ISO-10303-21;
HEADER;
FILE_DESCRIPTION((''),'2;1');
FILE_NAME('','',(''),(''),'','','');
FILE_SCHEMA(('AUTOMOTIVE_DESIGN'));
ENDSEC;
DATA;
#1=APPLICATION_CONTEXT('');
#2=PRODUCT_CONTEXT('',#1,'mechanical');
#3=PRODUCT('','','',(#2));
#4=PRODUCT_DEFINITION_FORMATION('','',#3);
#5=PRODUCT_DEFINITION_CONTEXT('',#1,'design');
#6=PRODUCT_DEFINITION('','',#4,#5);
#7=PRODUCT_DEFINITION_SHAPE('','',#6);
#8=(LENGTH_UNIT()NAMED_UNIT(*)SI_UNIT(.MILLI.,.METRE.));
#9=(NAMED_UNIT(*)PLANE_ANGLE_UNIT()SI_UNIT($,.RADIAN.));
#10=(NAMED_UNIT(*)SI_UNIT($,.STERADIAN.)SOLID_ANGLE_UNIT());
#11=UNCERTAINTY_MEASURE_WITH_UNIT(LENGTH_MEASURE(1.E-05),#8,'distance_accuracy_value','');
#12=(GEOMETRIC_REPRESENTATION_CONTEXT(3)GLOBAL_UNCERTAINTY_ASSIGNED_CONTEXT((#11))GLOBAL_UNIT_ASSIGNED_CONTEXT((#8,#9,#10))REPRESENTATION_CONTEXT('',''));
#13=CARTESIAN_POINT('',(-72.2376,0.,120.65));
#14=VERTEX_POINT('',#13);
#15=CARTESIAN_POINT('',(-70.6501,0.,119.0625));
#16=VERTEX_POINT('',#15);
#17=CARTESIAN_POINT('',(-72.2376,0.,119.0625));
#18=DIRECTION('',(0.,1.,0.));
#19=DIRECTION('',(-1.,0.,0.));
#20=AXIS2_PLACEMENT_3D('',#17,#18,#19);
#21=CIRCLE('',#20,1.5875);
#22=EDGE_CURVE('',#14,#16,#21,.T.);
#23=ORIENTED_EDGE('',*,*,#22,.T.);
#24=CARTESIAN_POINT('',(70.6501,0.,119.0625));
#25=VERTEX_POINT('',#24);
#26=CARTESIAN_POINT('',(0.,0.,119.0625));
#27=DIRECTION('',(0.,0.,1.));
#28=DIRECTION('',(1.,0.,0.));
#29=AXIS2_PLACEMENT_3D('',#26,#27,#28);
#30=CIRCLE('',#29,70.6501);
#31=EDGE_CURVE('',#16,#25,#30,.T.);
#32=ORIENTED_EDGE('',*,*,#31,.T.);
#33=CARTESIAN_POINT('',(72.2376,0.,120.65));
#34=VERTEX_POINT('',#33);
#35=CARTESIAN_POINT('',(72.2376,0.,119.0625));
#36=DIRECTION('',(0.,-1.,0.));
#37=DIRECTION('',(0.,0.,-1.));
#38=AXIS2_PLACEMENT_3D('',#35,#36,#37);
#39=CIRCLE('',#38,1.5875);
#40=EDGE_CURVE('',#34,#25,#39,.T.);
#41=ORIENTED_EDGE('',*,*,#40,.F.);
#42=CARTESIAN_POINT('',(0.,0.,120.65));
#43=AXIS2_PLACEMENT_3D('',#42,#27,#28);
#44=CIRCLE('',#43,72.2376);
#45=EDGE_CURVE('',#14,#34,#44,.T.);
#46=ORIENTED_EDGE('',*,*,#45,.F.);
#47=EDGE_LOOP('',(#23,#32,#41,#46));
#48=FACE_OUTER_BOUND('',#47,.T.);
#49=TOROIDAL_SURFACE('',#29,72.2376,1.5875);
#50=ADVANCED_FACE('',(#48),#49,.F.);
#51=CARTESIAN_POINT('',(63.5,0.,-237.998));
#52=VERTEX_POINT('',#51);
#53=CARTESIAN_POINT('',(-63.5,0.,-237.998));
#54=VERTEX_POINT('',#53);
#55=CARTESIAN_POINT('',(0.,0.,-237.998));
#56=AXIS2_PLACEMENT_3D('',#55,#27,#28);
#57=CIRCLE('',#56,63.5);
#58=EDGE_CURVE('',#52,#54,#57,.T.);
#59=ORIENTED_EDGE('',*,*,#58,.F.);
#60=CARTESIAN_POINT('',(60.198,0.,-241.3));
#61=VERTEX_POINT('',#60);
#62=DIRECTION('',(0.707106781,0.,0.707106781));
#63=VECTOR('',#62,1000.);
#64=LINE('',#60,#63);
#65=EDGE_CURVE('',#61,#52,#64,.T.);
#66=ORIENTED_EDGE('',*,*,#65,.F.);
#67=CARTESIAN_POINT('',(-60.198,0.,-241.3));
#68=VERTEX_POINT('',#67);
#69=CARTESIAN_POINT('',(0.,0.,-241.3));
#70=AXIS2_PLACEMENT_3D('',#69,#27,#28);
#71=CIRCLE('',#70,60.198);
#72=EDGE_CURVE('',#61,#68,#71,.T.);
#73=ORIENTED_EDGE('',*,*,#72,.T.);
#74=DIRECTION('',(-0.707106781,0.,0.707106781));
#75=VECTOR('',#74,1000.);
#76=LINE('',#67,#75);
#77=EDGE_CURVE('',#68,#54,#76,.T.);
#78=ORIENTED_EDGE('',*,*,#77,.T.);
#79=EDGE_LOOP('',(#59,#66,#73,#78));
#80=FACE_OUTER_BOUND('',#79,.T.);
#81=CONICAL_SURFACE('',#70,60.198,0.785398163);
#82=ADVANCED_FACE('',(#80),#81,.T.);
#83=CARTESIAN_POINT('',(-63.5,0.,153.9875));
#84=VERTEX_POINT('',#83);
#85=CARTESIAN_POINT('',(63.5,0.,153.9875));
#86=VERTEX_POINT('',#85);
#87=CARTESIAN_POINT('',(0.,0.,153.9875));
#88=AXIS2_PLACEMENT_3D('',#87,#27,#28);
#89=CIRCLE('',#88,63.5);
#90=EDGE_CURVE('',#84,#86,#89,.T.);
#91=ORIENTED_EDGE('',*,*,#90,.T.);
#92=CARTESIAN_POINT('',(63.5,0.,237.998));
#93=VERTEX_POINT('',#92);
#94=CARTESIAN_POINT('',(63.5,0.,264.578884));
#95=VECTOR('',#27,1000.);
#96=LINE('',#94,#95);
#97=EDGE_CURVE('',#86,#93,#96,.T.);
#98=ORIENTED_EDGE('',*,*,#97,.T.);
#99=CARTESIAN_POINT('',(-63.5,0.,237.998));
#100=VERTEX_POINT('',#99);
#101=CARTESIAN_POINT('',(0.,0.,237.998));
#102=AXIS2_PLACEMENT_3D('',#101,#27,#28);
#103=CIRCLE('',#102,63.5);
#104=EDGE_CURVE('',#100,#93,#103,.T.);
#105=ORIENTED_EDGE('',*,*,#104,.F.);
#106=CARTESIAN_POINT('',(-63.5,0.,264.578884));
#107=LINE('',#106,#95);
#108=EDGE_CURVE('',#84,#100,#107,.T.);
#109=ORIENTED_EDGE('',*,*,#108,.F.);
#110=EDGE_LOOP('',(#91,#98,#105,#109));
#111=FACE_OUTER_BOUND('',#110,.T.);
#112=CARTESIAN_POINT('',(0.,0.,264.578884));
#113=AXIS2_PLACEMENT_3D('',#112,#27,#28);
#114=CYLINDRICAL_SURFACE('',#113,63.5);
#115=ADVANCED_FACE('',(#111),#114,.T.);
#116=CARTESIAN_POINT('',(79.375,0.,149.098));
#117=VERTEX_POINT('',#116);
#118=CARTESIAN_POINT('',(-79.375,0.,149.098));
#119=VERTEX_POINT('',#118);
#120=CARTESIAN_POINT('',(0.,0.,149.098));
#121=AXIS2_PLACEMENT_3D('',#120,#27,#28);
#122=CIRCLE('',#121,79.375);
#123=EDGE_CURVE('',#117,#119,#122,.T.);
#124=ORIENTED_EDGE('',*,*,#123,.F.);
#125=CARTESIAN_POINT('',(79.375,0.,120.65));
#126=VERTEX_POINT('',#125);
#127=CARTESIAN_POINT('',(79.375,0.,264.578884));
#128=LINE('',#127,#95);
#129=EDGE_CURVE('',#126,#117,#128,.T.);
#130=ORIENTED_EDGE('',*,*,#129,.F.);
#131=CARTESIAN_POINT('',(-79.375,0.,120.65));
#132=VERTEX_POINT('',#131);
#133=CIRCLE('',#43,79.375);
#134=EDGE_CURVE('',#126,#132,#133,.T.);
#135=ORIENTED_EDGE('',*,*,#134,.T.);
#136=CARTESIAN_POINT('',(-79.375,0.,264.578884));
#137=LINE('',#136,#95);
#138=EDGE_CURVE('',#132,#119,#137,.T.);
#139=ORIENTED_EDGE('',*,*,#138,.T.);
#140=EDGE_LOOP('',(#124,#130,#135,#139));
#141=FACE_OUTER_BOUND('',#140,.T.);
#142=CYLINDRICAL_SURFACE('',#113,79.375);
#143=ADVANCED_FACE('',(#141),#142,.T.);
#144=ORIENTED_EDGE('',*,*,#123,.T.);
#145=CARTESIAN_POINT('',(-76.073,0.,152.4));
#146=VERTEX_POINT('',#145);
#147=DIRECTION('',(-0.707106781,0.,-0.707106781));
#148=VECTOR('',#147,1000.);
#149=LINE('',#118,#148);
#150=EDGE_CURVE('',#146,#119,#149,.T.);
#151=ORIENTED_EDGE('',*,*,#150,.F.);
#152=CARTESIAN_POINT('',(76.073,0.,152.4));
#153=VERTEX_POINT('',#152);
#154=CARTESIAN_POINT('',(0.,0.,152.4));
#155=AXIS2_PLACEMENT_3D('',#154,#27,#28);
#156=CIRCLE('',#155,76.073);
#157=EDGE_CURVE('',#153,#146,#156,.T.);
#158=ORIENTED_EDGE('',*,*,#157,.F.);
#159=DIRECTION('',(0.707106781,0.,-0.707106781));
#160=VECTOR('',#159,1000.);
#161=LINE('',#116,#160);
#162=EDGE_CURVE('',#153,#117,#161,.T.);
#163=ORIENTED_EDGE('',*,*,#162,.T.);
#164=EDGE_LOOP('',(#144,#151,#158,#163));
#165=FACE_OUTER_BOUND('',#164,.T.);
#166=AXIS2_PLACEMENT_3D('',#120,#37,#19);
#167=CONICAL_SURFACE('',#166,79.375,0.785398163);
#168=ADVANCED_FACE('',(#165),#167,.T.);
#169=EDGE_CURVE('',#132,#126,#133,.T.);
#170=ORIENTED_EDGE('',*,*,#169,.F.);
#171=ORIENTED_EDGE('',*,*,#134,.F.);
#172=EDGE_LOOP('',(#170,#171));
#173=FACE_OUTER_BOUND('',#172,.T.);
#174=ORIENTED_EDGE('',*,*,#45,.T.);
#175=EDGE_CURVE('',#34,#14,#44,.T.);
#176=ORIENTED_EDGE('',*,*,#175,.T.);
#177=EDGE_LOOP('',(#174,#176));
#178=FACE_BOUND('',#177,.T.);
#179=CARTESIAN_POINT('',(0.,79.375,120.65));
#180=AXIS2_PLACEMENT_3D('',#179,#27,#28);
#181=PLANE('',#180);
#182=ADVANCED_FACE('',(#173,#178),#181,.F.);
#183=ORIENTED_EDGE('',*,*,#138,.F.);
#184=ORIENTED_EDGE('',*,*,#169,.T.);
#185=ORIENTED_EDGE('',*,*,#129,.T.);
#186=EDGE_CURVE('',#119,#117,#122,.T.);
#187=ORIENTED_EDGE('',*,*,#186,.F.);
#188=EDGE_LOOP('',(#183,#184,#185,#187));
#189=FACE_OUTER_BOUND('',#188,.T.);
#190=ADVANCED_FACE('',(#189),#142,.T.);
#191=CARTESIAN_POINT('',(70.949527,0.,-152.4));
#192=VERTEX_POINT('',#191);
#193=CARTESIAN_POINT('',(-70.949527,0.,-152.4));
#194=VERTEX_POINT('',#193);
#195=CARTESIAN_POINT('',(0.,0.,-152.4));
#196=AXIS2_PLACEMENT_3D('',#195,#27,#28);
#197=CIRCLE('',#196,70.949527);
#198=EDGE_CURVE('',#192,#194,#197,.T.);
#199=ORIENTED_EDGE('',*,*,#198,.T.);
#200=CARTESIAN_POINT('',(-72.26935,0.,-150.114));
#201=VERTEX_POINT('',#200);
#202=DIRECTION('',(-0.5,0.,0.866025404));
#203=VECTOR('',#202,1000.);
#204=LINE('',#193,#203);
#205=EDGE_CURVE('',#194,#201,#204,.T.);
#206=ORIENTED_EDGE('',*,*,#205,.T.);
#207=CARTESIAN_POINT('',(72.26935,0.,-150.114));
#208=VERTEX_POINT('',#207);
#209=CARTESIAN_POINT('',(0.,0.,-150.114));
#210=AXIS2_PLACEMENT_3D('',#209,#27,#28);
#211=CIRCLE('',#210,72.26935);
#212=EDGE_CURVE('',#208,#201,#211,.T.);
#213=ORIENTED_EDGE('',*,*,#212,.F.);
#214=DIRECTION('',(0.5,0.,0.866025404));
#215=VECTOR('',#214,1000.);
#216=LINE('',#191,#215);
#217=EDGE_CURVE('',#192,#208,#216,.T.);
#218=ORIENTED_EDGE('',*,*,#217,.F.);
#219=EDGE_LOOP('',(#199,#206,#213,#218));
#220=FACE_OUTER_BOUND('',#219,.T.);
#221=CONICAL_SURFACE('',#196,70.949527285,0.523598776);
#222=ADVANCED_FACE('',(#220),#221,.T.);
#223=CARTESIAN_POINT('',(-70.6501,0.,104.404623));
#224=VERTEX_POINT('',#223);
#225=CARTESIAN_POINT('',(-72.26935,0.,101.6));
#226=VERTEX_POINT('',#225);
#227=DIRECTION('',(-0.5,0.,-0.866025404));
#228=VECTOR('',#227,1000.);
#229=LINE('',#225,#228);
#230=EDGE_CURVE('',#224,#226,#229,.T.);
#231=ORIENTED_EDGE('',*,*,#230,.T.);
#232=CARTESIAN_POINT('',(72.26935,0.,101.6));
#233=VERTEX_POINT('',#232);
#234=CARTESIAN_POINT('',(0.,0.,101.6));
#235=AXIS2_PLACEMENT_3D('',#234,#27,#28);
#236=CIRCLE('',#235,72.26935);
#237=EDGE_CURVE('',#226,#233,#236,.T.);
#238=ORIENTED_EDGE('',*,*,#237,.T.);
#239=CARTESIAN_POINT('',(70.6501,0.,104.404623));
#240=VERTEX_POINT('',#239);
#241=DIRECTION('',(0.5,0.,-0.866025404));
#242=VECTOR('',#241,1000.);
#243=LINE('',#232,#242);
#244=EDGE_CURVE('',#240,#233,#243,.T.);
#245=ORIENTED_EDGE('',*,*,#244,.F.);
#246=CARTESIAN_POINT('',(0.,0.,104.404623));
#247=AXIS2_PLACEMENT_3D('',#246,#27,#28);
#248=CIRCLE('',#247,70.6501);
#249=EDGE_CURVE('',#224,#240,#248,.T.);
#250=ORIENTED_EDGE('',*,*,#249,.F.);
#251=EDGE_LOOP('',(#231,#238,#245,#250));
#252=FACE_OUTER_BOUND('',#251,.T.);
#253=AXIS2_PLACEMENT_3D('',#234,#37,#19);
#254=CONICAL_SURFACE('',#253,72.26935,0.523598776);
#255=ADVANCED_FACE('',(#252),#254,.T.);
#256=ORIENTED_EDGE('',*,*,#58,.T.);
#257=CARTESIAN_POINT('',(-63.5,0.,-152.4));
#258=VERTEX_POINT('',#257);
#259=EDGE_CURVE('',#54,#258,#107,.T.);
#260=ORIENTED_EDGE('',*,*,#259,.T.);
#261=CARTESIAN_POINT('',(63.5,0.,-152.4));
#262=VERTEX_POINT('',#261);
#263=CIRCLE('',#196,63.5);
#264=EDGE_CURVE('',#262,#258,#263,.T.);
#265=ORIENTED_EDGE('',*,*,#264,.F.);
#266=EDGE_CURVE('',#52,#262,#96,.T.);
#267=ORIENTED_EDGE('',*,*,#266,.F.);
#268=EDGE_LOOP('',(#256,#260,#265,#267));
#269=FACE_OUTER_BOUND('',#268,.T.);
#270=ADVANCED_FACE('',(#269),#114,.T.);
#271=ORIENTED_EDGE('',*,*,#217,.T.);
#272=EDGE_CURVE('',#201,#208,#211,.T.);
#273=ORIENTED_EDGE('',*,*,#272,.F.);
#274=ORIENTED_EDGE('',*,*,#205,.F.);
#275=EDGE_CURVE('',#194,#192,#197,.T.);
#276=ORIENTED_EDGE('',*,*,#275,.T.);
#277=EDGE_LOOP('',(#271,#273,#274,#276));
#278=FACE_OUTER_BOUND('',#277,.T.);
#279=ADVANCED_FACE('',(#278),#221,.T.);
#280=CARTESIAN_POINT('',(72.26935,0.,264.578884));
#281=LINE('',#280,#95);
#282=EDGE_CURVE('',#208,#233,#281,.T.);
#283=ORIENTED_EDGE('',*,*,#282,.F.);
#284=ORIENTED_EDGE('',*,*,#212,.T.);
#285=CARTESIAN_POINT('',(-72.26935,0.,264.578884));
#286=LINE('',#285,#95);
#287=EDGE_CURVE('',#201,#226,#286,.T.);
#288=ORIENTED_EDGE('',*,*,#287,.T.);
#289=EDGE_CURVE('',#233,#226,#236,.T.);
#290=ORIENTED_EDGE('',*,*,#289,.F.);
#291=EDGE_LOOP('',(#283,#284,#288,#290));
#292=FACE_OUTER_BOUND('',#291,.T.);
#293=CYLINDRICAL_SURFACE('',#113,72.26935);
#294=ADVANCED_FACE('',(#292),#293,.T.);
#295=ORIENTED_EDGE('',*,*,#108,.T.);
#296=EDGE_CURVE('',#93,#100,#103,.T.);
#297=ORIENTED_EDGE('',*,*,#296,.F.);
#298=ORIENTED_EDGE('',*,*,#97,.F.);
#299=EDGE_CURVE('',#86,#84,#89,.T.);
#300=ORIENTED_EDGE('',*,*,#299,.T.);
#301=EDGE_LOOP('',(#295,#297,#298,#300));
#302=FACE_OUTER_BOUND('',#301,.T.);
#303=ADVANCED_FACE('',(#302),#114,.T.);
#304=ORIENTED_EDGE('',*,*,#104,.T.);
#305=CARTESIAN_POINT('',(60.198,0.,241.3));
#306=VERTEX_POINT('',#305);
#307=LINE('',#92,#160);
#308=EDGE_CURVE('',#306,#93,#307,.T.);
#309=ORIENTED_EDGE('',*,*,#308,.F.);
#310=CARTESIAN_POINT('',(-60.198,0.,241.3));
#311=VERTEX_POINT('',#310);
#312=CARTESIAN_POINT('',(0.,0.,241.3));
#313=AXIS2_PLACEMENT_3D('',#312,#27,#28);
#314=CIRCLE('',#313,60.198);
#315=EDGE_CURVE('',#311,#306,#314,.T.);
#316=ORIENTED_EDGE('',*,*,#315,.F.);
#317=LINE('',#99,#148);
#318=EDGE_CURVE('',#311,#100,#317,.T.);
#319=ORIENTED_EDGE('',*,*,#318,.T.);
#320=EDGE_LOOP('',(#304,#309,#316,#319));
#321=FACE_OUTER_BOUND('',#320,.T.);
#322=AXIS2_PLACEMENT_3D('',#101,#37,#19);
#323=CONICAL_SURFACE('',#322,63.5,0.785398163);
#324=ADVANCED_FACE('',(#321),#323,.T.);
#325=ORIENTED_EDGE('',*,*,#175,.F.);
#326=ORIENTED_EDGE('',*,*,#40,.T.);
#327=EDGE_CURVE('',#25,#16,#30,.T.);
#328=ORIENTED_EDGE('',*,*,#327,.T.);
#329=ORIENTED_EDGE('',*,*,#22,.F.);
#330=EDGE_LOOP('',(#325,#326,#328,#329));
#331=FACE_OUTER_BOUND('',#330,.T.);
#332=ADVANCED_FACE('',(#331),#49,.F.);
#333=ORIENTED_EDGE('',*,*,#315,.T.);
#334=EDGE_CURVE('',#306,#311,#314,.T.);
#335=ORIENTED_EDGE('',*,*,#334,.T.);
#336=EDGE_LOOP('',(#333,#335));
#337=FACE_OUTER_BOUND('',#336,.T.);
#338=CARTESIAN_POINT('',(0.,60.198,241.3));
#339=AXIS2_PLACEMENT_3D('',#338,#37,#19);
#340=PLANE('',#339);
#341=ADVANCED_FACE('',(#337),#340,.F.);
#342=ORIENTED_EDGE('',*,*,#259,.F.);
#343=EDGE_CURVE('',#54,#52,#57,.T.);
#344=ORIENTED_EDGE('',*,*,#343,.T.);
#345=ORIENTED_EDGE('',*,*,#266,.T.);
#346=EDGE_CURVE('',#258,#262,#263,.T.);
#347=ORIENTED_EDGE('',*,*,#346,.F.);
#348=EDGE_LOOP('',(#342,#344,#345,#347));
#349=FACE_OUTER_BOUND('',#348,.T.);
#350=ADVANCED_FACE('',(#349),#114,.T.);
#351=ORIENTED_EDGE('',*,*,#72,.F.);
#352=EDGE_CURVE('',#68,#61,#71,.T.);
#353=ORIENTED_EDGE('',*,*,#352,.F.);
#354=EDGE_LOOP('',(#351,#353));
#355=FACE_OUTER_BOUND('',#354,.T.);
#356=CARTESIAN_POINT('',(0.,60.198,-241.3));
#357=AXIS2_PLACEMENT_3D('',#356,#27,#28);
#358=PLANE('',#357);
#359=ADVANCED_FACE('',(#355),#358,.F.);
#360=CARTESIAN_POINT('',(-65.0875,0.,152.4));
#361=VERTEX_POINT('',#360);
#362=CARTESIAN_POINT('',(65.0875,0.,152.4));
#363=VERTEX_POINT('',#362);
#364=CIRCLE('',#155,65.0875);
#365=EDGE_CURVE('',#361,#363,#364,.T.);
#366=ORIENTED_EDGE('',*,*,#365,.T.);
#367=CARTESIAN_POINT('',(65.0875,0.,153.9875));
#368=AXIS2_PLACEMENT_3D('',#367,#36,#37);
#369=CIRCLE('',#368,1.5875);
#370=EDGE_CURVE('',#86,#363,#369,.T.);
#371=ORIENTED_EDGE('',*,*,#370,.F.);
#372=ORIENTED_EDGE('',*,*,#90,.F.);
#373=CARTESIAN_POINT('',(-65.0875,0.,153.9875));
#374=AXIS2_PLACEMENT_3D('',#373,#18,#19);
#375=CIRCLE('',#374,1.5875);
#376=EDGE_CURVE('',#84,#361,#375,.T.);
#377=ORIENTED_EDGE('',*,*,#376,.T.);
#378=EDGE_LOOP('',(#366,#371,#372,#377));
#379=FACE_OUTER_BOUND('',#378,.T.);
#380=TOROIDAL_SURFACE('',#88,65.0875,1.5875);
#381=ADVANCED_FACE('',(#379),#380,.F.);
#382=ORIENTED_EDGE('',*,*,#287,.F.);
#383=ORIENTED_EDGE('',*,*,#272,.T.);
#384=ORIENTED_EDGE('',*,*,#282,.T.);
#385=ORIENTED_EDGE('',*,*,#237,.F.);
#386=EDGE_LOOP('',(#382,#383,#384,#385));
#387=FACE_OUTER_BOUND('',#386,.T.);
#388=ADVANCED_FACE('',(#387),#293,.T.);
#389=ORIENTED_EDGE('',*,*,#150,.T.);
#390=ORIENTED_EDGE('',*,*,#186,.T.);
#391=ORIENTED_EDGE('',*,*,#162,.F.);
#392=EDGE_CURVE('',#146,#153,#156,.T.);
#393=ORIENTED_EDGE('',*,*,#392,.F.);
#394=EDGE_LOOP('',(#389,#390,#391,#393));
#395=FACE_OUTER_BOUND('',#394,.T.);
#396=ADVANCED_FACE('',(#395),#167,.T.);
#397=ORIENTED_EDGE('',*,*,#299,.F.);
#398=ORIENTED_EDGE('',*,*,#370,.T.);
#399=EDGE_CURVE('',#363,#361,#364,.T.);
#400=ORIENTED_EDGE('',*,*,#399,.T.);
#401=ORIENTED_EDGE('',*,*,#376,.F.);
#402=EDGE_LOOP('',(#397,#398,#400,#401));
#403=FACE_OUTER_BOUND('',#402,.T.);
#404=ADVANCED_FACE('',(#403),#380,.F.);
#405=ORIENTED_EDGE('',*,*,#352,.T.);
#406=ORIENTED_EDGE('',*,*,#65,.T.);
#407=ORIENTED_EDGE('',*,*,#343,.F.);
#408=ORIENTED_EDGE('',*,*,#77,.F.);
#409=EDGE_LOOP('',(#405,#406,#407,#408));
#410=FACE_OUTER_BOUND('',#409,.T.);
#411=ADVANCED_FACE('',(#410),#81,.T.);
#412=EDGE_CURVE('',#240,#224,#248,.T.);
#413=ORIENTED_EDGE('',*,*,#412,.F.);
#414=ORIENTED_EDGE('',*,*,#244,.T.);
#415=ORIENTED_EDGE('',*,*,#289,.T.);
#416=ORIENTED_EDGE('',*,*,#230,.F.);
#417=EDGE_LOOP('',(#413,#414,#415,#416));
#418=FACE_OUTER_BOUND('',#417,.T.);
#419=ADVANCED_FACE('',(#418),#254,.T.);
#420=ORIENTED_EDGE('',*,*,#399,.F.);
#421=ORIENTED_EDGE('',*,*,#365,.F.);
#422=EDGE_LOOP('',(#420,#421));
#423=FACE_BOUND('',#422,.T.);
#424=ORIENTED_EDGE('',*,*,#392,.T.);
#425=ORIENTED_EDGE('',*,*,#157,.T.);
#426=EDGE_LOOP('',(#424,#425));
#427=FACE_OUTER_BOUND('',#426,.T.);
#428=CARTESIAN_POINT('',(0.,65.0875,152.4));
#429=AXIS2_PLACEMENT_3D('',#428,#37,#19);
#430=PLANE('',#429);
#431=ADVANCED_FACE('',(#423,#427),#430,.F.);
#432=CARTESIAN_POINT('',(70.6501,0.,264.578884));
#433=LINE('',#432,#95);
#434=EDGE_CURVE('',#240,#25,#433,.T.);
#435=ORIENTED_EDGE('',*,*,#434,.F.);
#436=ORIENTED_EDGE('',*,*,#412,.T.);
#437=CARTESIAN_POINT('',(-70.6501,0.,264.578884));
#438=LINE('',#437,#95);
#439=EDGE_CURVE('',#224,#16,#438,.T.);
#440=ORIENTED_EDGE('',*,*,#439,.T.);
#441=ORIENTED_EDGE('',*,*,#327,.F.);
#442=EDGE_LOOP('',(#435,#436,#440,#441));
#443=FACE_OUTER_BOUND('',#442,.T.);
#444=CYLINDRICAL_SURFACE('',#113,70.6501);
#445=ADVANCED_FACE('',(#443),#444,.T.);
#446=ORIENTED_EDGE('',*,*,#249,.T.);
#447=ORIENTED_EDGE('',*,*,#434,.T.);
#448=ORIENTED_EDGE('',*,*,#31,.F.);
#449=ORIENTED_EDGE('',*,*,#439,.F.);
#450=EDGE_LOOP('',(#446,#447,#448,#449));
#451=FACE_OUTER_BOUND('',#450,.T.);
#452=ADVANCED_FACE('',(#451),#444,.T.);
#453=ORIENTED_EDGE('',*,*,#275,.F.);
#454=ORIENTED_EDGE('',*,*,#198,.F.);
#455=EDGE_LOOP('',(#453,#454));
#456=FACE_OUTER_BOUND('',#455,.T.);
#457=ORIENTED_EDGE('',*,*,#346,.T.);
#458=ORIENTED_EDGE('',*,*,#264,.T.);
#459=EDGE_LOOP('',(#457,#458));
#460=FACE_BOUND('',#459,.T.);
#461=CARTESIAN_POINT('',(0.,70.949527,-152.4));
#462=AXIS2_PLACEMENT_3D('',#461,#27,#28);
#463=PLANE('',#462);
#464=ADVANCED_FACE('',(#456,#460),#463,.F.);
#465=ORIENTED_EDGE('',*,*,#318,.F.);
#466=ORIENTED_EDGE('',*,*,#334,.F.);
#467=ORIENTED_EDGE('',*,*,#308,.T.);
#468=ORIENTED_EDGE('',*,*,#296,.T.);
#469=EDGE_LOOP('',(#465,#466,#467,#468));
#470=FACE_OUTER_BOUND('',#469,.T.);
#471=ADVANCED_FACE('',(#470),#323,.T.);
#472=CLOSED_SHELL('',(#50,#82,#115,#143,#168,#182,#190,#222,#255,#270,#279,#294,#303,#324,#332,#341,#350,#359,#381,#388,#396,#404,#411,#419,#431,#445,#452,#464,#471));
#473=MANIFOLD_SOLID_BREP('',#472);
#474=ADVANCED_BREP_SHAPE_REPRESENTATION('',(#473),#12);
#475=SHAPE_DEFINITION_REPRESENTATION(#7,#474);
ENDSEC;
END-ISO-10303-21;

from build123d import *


with BuildPart() as part:
    # Sketch1 → Revolve1 (revolve)
    with BuildSketch(Plane(origin=(0, 0, 0), x_dir=(0, 0, -1), z_dir=(1, 0, 0)), mode=Mode.PRIVATE) as revolve1_sk:
        with BuildLine():
            Line((-237.998, 63.5), (-153.9875, 63.5))
            ThreePointArc((-153.9875, 63.5), (-152.864967985, 63.964967985), (-152.4, 65.0875))
            Line((-152.4, 65.0875), (-152.4, 76.073))
            Line((-152.4, 76.073), (-149.098, 79.375))
            Line((-149.098, 79.375), (-120.65, 79.375))
            Line((-120.65, 79.375), (-120.65, 72.2376))
            ThreePointArc((-120.65, 72.2376), (-120.185032015, 71.115067985), (-119.0625, 70.6501))
            Line((-119.0625, 70.6501), (-104.40462327, 70.6501))
            Line((-104.40462327, 70.6501), (-101.6, 72.26935))
            Line((-101.6, 72.26935), (150.114, 72.26935))
            Line((150.114, 72.26935), (152.4, 70.949527285))
            Line((152.4, 70.949527285), (152.4, 63.5))
            Line((152.4, 63.5), (237.998, 63.5))
            Line((237.998, 63.5), (241.3, 60.198))
            Line((241.3, 60.198), (241.3, 0))
            Line((241.3, 0), (-241.3, 0))
            Line((-241.3, 0), (-241.3, 60.198))
            Line((-241.3, 60.198), (-237.998, 63.5))
        make_face()
    revolve(revolve1_sk.sketch.rotate(Axis((0, 0, 264.578884175), (0, 0, -1)), 90), axis=Axis((0, 0, 264.578884175), (0, 0, -1)))


solid = part.part
